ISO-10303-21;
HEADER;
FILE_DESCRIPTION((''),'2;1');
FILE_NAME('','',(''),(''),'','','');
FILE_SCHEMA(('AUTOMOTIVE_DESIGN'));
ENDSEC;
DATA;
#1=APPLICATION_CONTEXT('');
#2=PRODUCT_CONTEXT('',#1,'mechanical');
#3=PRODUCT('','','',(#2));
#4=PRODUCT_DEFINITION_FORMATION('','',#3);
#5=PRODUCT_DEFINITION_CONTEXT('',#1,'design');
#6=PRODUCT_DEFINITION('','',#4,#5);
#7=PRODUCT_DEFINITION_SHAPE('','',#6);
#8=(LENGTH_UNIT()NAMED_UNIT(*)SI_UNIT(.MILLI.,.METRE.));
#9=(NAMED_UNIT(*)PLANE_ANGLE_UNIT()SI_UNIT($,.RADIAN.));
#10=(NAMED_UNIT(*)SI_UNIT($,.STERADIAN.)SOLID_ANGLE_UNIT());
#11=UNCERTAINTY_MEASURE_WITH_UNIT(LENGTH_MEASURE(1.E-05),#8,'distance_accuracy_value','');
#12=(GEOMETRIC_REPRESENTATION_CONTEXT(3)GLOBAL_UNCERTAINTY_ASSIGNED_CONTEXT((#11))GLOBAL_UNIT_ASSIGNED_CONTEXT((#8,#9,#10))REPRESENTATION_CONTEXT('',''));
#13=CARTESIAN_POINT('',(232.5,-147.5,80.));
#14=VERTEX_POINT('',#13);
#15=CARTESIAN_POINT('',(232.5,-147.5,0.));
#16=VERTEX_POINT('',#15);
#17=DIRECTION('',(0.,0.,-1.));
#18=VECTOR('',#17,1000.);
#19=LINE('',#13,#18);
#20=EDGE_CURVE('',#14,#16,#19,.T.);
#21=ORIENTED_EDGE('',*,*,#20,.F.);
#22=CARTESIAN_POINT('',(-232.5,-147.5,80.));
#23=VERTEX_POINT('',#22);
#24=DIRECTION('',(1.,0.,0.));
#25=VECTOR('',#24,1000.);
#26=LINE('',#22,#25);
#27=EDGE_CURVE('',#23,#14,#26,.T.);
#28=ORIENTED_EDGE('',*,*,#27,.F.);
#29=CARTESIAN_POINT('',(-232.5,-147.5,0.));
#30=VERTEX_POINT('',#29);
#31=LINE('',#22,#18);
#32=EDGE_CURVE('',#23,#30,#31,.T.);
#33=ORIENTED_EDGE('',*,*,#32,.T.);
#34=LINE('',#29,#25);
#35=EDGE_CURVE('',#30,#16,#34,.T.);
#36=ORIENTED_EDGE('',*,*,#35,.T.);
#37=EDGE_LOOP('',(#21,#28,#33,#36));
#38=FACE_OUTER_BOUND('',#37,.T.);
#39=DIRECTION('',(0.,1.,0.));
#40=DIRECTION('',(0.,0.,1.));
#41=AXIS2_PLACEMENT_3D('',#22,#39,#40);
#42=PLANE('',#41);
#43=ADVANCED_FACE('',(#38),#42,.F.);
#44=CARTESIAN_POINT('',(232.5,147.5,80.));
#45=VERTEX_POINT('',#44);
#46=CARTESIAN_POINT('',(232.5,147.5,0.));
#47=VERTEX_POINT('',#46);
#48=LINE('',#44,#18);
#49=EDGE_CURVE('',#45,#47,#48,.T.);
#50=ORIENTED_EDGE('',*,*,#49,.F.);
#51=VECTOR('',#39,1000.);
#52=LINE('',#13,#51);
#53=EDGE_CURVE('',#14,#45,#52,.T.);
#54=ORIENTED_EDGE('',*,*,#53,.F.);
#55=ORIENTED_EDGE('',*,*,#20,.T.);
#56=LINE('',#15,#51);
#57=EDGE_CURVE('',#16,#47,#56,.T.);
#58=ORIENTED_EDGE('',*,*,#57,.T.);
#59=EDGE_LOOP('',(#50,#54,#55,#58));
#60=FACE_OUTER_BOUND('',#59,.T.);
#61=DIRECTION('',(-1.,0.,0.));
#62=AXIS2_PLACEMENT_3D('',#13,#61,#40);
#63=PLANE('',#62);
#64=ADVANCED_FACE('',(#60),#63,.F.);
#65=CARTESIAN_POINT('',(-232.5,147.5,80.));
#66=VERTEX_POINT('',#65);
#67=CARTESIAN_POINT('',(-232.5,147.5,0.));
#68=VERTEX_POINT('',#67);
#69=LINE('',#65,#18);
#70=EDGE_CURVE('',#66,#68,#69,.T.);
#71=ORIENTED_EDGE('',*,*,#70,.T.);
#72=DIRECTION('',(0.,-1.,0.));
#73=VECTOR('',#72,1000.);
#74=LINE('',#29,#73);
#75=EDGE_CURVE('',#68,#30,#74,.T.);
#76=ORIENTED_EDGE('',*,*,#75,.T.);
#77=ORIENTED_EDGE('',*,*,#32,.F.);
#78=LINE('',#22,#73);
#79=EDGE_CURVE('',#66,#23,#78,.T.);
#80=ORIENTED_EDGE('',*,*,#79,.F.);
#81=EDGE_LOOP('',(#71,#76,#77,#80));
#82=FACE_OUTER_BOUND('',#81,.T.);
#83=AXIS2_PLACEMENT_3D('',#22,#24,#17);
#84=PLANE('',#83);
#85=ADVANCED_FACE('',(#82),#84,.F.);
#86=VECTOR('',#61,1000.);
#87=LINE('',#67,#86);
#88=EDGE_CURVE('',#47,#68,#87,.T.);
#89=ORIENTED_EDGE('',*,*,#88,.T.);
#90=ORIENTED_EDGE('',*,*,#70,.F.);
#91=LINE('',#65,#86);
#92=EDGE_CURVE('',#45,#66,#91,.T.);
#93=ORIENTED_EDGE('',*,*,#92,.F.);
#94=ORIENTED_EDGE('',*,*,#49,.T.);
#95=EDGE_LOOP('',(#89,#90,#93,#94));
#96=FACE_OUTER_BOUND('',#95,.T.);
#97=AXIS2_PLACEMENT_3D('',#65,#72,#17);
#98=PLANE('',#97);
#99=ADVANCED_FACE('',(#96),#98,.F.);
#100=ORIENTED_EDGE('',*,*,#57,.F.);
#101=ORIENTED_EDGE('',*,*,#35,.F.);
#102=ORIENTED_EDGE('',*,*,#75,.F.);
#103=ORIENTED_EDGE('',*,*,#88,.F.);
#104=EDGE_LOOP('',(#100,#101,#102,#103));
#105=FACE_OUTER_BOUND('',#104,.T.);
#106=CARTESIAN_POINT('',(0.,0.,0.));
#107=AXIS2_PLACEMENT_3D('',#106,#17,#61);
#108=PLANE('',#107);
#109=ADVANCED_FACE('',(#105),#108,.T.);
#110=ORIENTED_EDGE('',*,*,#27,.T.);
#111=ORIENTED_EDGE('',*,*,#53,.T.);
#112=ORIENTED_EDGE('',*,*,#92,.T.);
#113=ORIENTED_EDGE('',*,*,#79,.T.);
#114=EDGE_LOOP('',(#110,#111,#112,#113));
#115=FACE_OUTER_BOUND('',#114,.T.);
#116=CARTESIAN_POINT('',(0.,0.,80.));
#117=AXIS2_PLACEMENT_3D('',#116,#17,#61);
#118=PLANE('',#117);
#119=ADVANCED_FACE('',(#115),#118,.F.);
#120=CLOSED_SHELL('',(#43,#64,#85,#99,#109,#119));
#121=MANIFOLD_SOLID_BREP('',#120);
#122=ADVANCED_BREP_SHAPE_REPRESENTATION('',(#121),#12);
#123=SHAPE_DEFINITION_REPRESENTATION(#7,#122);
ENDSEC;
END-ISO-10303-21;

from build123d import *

# Parameters (mm, degrees)
SKETCH_1_W      = 465
SKETCH_1_H      = 295
EXTRUDE_1_DEPTH = 80


with BuildPart() as part:
    # 草图1 → 凸台-拉伸1 (new body)
    with BuildSketch(Plane.XY):
        Rectangle(SKETCH_1_W, SKETCH_1_H)
    extrude(amount=EXTRUDE_1_DEPTH)


solid = part.part
